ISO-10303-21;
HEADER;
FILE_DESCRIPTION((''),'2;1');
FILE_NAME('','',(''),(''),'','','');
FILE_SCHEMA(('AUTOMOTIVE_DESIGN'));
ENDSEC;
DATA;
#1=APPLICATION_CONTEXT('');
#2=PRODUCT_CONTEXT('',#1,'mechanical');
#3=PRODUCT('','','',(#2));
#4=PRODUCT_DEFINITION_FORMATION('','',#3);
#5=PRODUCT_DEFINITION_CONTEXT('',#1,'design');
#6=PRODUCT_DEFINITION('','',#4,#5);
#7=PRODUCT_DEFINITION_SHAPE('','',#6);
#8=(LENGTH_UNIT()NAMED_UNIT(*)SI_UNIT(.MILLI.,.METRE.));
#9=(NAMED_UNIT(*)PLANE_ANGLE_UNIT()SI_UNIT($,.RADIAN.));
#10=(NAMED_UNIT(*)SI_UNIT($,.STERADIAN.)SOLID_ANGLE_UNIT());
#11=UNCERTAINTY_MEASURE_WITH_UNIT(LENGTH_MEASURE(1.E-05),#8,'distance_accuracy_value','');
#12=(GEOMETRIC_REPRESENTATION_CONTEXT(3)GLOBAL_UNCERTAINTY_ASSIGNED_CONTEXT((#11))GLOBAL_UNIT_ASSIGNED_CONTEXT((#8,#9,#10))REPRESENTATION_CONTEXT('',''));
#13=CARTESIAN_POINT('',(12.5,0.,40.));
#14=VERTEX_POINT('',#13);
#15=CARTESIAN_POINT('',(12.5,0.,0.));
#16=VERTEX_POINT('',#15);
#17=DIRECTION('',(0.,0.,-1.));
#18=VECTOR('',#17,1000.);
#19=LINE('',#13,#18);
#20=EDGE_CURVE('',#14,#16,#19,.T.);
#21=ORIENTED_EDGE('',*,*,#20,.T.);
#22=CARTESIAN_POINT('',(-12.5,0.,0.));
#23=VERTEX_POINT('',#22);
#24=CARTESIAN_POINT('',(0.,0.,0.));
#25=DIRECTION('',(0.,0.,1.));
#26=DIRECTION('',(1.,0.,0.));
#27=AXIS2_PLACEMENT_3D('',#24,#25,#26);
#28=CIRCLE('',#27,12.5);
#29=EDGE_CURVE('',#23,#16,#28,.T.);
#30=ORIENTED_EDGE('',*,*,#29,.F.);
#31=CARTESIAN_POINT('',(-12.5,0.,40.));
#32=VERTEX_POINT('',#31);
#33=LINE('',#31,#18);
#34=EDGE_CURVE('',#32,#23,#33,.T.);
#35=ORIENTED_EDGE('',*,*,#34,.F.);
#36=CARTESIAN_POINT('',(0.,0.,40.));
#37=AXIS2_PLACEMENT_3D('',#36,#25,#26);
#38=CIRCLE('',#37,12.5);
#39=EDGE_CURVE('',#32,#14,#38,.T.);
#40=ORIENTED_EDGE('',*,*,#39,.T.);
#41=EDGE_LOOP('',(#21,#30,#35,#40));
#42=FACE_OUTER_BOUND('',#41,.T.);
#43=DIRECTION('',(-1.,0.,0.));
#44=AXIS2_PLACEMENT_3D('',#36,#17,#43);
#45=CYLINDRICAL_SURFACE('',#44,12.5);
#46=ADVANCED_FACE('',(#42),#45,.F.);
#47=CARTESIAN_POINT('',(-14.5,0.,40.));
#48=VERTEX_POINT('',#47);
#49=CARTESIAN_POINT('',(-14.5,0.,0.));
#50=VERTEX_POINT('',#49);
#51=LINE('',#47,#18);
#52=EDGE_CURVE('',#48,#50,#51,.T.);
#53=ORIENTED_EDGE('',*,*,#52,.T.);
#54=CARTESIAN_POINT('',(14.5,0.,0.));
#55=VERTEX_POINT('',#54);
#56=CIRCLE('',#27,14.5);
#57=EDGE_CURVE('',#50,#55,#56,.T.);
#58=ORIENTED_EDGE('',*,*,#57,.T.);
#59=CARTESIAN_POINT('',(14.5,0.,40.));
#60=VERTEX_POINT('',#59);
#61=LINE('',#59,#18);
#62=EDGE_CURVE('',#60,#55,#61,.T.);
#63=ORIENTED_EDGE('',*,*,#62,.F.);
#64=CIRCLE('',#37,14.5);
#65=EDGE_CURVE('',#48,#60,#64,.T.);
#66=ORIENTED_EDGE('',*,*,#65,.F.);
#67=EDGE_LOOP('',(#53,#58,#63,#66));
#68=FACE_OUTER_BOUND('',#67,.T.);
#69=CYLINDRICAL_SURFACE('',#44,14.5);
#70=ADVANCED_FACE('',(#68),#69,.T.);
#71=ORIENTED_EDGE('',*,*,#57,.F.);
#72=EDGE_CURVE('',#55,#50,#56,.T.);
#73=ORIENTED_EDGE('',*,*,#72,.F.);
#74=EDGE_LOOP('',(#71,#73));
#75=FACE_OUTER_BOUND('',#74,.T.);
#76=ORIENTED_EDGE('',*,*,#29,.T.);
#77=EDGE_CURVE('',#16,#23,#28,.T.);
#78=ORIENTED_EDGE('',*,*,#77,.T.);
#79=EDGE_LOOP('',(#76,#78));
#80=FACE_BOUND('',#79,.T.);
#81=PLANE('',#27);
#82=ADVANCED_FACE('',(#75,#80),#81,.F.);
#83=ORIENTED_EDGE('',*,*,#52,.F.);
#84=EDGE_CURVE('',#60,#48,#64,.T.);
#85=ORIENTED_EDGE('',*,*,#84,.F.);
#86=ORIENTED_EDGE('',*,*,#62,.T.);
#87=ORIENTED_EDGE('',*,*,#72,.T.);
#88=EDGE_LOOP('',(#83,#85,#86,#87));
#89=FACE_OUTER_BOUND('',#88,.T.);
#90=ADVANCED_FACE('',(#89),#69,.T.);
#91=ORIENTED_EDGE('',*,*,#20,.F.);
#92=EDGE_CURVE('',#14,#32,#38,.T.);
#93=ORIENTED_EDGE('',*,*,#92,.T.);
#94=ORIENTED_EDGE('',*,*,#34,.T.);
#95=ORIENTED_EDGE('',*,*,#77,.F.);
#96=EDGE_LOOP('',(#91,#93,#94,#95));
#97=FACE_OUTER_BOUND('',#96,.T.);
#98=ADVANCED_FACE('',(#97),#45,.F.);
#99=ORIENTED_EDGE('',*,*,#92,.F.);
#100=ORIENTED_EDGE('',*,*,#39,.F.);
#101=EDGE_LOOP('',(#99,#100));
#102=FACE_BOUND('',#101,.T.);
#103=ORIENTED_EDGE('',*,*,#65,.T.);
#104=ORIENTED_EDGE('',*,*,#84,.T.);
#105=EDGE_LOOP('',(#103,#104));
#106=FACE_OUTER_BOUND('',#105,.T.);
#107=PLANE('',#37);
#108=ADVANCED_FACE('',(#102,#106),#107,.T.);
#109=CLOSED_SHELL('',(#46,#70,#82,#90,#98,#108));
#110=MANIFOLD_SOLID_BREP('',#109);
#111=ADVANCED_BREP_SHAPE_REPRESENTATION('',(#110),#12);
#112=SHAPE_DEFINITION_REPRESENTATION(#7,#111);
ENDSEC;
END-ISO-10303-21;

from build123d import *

# Parameters (mm, degrees)
SKETCH1_R           = 14.5
SKETCH1_R_2         = 12.5
BOSS_EXTRUDE1_DEPTH = 40


with BuildPart() as part:
    # Sketch1 → Boss-Extrude1 (new body)
    with BuildSketch(Plane.XY):
        Circle(SKETCH1_R)
        Circle(SKETCH1_R_2, mode=Mode.SUBTRACT)
    extrude(amount=BOSS_EXTRUDE1_DEPTH)


solid = part.part
